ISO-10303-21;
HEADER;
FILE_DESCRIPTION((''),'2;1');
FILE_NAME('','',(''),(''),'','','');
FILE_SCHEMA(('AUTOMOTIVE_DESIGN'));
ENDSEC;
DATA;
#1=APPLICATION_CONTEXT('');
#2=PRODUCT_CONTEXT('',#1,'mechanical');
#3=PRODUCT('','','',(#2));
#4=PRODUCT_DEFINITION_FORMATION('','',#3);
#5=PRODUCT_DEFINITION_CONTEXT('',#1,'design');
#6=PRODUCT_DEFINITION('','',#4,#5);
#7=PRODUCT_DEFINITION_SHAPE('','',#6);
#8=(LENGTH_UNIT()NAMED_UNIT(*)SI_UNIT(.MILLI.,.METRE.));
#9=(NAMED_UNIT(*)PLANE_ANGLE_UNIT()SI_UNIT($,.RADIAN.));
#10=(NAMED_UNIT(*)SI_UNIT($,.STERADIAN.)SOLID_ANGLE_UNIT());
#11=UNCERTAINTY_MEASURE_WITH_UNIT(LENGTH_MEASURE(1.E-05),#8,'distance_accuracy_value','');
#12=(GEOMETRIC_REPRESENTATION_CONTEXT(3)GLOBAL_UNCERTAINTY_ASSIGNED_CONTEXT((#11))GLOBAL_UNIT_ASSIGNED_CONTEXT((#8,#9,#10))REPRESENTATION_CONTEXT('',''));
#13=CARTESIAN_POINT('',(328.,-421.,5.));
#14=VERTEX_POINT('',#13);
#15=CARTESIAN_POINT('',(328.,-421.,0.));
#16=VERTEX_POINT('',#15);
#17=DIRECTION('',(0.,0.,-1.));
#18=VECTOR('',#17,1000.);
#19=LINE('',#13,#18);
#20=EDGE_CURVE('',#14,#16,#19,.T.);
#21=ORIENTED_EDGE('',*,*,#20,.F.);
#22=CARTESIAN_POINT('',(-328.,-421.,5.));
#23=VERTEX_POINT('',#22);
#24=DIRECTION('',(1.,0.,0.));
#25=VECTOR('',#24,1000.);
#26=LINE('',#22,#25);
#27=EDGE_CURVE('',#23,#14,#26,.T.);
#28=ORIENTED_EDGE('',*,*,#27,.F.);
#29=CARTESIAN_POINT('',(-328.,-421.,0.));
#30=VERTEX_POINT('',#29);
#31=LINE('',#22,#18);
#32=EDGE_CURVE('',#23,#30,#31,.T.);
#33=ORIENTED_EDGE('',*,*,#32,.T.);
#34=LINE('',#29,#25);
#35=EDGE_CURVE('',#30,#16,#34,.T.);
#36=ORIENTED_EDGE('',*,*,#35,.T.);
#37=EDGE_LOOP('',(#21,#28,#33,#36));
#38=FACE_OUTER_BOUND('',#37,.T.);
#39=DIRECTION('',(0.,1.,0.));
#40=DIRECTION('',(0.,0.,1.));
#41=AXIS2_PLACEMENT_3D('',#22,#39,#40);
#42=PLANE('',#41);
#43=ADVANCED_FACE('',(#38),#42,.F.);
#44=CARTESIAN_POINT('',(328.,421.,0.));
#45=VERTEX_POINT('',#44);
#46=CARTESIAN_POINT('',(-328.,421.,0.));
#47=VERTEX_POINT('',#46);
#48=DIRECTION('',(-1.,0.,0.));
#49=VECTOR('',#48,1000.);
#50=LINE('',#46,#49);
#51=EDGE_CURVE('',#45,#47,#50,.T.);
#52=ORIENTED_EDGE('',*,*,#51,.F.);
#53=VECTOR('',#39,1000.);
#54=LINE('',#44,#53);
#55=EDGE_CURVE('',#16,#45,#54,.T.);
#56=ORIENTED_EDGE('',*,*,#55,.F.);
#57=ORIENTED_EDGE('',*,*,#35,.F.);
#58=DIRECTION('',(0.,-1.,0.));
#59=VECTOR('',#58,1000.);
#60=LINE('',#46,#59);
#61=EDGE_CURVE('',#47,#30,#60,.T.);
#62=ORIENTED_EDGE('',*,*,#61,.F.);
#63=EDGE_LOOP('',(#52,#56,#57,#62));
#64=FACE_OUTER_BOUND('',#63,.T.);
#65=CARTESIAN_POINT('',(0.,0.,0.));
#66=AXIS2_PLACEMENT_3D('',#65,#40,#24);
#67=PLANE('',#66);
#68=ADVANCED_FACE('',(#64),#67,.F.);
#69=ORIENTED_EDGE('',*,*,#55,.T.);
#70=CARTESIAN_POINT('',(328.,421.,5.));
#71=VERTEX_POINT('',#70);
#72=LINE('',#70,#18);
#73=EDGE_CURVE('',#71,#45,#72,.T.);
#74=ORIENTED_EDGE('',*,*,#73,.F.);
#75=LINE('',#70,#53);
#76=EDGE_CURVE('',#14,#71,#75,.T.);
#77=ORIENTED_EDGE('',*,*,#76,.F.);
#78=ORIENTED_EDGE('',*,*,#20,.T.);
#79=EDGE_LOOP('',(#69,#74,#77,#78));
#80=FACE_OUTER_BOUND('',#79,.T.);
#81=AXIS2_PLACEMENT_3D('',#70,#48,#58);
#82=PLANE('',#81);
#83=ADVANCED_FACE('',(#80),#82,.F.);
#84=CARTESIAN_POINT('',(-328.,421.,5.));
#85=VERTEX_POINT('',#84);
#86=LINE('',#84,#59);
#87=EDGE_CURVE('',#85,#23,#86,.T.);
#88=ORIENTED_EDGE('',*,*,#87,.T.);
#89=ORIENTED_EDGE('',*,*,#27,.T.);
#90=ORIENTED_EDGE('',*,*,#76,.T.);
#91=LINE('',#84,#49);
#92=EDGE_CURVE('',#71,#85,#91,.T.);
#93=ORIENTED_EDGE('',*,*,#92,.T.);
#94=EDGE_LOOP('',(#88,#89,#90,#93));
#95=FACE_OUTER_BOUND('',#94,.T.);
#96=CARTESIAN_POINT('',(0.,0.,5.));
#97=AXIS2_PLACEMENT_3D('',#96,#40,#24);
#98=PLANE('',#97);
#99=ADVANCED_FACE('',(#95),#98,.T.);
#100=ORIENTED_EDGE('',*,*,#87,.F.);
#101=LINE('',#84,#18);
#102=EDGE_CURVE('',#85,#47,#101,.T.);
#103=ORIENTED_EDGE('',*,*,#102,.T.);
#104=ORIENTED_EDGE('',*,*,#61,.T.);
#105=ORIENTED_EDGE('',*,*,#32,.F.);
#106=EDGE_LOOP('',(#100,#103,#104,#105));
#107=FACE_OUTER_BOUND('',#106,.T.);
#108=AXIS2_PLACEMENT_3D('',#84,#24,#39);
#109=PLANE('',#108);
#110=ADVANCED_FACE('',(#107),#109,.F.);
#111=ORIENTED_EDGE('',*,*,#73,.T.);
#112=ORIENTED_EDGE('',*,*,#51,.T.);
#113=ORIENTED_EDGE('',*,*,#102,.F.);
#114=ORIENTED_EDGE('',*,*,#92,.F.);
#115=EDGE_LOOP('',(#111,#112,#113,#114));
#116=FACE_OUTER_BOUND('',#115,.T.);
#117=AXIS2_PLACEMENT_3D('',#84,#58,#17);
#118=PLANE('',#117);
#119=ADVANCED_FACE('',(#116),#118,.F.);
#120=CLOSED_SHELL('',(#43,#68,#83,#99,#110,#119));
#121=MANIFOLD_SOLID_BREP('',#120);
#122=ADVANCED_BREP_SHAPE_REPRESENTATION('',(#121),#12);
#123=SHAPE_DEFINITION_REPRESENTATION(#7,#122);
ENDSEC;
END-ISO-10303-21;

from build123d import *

# Parameters (mm, degrees)
SKETCH_1_W      = 656
SKETCH_1_H      = 842
EXTRUDE_1_DEPTH = 5


with BuildPart() as part:
    # 草图1 → 凸台-拉伸1 (new body)
    with BuildSketch(Plane.XY):
        Rectangle(SKETCH_1_W, SKETCH_1_H)
    extrude(amount=EXTRUDE_1_DEPTH)


solid = part.part
